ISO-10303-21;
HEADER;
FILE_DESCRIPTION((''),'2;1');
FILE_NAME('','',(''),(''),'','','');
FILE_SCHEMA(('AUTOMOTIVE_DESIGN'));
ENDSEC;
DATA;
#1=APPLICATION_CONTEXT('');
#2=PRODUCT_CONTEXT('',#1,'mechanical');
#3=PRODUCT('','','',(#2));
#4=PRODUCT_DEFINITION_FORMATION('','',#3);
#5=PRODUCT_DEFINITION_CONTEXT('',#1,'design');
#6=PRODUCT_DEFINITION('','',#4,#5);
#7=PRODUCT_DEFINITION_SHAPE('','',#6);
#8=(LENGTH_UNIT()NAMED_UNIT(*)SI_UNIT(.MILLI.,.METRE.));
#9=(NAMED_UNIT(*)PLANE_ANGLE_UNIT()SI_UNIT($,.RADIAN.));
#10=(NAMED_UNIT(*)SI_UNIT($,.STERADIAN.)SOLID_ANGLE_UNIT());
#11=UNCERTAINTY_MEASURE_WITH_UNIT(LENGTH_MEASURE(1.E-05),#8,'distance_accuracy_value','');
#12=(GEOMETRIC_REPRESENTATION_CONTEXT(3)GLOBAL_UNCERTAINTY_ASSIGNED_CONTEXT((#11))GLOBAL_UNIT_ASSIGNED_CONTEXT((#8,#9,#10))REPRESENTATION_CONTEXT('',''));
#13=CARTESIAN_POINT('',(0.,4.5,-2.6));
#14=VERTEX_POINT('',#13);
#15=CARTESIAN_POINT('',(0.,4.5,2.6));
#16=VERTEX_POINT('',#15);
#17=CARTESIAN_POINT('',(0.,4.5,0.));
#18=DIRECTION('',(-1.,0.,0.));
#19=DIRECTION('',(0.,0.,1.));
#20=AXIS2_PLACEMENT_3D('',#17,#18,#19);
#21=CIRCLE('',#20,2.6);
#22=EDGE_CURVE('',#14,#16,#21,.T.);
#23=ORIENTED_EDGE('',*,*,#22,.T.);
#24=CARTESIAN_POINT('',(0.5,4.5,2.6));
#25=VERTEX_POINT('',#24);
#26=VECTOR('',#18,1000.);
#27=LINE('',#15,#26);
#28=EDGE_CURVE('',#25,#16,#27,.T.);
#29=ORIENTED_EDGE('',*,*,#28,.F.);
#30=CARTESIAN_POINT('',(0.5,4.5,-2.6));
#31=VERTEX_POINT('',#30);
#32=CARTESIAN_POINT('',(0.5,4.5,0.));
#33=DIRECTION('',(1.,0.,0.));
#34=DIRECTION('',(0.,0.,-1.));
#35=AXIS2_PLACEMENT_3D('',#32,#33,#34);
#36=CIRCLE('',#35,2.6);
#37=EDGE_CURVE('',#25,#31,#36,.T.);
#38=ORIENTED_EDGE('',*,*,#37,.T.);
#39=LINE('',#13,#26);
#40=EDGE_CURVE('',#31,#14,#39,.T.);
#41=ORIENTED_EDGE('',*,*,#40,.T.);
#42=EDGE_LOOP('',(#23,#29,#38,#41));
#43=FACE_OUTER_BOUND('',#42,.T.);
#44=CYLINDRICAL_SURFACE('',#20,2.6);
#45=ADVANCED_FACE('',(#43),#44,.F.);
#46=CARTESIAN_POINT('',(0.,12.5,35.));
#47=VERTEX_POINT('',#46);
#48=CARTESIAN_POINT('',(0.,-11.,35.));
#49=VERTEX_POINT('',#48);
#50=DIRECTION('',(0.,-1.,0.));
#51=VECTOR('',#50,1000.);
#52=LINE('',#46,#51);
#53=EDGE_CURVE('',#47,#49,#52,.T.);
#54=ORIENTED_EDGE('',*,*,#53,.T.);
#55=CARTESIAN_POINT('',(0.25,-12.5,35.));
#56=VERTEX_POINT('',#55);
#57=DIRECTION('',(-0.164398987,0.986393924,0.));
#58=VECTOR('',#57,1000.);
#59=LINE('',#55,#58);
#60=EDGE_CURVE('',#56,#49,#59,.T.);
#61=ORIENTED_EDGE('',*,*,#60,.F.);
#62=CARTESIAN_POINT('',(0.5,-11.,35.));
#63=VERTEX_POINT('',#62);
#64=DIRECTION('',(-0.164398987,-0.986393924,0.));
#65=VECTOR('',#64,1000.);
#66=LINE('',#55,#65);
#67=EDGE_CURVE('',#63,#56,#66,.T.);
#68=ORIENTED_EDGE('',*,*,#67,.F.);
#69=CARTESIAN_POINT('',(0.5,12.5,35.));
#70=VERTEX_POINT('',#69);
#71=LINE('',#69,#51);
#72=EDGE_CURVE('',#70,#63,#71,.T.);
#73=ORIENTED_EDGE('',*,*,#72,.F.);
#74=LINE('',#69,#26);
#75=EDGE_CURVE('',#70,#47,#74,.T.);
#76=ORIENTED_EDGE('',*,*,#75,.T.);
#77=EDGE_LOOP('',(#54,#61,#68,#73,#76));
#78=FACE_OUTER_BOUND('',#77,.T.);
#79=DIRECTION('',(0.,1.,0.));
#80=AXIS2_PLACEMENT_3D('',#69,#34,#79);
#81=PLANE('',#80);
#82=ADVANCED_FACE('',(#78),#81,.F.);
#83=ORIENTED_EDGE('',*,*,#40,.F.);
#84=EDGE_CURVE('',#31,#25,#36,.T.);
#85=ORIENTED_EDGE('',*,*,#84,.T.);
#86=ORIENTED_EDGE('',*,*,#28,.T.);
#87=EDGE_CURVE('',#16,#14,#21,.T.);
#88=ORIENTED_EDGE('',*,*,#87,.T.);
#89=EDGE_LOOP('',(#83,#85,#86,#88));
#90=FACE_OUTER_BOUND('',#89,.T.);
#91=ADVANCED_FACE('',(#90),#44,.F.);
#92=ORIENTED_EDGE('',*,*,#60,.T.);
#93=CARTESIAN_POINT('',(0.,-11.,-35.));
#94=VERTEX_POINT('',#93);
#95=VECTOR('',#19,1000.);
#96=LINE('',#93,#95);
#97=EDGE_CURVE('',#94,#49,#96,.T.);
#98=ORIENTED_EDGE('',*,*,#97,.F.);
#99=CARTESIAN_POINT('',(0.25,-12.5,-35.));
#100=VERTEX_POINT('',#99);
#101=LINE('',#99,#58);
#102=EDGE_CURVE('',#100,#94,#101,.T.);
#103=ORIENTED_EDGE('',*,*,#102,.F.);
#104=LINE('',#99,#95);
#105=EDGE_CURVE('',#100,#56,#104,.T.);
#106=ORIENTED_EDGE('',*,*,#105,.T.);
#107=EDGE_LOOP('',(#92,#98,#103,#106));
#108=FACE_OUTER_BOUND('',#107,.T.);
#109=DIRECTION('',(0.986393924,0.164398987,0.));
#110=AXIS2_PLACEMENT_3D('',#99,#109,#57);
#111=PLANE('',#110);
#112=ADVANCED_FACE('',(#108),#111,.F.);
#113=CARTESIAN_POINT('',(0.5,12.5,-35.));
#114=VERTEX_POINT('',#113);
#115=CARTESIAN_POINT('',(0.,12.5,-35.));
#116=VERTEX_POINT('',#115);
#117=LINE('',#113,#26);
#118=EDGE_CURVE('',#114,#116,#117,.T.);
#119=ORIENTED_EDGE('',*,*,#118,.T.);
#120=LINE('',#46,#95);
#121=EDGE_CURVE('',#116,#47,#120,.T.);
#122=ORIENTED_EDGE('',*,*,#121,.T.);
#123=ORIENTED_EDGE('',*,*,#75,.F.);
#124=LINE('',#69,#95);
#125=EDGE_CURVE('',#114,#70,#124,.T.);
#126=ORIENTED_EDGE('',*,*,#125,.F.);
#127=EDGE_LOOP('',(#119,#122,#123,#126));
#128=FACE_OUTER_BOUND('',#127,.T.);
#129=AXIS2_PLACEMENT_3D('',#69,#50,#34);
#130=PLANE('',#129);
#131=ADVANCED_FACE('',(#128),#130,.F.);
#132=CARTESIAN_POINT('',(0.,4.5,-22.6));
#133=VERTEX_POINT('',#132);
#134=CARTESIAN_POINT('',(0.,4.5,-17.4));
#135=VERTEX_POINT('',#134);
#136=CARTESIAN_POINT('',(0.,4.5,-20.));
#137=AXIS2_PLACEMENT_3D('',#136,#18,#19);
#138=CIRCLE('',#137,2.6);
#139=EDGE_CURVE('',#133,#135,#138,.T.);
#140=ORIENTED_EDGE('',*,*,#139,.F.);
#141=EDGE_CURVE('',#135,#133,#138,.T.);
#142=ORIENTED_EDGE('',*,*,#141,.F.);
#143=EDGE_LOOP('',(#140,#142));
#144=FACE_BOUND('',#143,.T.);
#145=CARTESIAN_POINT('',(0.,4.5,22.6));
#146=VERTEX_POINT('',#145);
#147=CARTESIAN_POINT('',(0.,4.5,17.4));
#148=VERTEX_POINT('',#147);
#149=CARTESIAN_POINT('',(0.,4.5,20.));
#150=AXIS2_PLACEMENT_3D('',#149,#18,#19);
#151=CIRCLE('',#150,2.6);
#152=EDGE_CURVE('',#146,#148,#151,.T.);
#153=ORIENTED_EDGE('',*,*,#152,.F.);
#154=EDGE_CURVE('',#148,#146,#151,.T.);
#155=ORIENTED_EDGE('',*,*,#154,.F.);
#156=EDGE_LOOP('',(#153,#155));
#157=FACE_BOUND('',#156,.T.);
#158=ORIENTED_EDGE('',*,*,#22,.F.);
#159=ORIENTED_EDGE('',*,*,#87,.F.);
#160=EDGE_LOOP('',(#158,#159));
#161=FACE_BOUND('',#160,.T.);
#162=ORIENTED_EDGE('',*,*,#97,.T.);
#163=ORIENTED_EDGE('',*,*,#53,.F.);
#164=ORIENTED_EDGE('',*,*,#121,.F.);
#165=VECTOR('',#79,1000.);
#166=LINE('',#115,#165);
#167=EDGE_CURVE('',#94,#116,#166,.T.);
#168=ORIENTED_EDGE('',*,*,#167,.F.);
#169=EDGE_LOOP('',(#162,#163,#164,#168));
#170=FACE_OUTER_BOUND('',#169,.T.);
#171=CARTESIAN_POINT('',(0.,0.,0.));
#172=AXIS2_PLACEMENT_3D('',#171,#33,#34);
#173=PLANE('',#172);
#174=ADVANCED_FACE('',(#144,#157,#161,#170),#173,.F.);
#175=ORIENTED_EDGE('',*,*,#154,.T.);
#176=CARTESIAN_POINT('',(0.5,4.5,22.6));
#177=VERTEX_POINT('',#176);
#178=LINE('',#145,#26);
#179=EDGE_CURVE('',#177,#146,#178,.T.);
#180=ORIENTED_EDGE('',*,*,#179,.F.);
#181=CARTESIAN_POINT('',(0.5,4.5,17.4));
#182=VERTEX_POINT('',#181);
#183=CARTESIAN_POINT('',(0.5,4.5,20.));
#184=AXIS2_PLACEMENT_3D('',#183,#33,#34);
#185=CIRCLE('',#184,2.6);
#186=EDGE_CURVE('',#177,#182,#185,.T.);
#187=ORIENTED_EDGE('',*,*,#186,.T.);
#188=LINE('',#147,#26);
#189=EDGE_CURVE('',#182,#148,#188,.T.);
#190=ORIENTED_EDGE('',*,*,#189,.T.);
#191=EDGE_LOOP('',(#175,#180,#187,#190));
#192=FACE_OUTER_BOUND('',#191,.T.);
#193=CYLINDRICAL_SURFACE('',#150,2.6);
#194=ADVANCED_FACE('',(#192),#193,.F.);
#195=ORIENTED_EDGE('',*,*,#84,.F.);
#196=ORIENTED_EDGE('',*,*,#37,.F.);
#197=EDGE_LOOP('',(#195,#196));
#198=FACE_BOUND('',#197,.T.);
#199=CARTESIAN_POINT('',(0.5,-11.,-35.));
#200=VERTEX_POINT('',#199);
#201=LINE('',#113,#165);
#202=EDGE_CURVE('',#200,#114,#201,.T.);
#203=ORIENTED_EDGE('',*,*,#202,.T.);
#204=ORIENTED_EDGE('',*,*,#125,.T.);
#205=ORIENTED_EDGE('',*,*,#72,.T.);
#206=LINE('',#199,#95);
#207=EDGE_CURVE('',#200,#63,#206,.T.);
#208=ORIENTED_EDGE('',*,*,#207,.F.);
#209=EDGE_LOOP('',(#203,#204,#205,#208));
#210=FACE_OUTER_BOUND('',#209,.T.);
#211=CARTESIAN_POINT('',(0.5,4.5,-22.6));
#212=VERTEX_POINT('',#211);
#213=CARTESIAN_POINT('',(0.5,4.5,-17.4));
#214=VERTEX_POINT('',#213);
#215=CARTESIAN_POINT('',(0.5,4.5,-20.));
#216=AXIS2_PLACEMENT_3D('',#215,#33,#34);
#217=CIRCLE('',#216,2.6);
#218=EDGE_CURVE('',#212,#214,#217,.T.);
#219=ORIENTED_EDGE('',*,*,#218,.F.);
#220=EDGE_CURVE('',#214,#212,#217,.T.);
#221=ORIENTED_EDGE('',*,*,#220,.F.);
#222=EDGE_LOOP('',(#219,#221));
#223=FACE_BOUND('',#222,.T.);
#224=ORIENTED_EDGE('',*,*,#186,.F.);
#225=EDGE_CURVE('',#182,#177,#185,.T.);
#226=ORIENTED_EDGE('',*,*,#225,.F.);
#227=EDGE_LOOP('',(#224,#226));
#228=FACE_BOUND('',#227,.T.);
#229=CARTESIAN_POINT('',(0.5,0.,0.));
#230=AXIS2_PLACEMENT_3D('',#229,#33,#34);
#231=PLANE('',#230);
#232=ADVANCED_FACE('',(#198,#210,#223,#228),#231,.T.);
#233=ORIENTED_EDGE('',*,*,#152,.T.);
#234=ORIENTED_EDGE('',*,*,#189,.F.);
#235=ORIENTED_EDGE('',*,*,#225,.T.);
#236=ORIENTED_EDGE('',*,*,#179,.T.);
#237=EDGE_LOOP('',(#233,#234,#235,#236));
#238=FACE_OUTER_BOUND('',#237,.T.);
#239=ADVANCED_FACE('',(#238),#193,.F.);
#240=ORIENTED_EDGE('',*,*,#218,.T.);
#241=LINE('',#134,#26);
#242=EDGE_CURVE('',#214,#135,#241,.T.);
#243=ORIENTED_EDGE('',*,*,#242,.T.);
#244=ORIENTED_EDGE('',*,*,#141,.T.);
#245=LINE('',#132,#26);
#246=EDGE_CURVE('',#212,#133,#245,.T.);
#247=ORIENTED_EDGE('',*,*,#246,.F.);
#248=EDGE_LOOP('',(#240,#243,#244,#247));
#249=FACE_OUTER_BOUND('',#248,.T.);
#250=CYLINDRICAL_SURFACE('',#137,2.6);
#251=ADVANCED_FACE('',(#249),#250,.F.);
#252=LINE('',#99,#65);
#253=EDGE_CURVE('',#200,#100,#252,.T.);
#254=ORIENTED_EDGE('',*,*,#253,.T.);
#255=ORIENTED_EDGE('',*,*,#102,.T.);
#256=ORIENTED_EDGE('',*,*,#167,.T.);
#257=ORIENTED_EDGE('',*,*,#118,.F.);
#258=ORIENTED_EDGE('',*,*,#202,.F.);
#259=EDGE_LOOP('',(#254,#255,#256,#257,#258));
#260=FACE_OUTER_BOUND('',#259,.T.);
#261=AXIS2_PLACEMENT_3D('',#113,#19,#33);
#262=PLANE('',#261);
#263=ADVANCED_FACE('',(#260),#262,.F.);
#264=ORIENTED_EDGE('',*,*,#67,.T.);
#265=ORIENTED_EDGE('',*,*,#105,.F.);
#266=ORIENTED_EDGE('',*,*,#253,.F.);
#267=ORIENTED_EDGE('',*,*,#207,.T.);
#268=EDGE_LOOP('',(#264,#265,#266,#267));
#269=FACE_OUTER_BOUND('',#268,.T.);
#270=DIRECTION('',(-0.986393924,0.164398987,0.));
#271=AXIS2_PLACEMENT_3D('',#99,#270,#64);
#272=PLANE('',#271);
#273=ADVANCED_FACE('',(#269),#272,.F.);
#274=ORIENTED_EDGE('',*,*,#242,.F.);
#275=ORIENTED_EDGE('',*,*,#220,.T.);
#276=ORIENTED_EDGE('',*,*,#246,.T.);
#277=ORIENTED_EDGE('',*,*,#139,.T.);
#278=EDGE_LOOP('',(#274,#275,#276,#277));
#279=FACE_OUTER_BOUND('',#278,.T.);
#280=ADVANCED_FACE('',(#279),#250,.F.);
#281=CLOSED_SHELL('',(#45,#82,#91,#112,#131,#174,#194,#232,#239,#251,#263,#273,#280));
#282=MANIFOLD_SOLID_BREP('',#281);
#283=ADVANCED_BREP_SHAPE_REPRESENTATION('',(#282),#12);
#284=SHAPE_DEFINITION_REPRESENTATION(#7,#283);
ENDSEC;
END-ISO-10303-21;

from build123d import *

# Parameters (mm, degrees)
SKETCH_1_W                  = 70
SKETCH_1_H                  = 25
EXTRUDE_1_DEPTH             = 0.5
CUT_EXTRUDE_1_DEPTH         = 72.109071151
HOLE_WIZARD_5_2_5_2_1_D     = 5.2
HOLE_WIZARD_5_2_5_2_1_DEPTH = 19.75
HOLE_WIZARD_5_2_5_2_1_TIP   = 1.562237609


with BuildPart() as part:
    # 草图1 → 凸台-拉伸1 (new body)
    with BuildSketch(Plane(origin=(0, 0, 0), x_dir=(0, 0, -1), z_dir=(1, 0, 0))):
        Rectangle(SKETCH_1_W, SKETCH_1_H)
    extrude(amount=EXTRUDE_1_DEPTH)

    # 草图2 → 切除-拉伸1 (cut, through all)
    with BuildSketch(Plane.XY.offset(35)):
        Polygon((0.25, -12.5), (0, -11), (-1.209013091, -11.201502182), (-0.510365148, -13.117899248), (1.363353431, -13.117899248), (1.198992152, -10.8497136), (0.5, -11), align=None)
    extrude(amount=-CUT_EXTRUDE_1_DEPTH, mode=Mode.SUBTRACT)

    # Ø5.2 (5.2) 直径孔1
    with Locations(Plane.ZY):
        with Locations((-20, 4.5), (0, 4.5), (20, 4.5)):
            Hole(HOLE_WIZARD_5_2_5_2_1_D / 2, depth=HOLE_WIZARD_5_2_5_2_1_DEPTH)
            with Locations((0, 0, -(HOLE_WIZARD_5_2_5_2_1_DEPTH + HOLE_WIZARD_5_2_5_2_1_TIP / 2))):  # 118° drill point
                Cone(0, HOLE_WIZARD_5_2_5_2_1_D / 2, HOLE_WIZARD_5_2_5_2_1_TIP, mode=Mode.SUBTRACT)


solid = part.part
